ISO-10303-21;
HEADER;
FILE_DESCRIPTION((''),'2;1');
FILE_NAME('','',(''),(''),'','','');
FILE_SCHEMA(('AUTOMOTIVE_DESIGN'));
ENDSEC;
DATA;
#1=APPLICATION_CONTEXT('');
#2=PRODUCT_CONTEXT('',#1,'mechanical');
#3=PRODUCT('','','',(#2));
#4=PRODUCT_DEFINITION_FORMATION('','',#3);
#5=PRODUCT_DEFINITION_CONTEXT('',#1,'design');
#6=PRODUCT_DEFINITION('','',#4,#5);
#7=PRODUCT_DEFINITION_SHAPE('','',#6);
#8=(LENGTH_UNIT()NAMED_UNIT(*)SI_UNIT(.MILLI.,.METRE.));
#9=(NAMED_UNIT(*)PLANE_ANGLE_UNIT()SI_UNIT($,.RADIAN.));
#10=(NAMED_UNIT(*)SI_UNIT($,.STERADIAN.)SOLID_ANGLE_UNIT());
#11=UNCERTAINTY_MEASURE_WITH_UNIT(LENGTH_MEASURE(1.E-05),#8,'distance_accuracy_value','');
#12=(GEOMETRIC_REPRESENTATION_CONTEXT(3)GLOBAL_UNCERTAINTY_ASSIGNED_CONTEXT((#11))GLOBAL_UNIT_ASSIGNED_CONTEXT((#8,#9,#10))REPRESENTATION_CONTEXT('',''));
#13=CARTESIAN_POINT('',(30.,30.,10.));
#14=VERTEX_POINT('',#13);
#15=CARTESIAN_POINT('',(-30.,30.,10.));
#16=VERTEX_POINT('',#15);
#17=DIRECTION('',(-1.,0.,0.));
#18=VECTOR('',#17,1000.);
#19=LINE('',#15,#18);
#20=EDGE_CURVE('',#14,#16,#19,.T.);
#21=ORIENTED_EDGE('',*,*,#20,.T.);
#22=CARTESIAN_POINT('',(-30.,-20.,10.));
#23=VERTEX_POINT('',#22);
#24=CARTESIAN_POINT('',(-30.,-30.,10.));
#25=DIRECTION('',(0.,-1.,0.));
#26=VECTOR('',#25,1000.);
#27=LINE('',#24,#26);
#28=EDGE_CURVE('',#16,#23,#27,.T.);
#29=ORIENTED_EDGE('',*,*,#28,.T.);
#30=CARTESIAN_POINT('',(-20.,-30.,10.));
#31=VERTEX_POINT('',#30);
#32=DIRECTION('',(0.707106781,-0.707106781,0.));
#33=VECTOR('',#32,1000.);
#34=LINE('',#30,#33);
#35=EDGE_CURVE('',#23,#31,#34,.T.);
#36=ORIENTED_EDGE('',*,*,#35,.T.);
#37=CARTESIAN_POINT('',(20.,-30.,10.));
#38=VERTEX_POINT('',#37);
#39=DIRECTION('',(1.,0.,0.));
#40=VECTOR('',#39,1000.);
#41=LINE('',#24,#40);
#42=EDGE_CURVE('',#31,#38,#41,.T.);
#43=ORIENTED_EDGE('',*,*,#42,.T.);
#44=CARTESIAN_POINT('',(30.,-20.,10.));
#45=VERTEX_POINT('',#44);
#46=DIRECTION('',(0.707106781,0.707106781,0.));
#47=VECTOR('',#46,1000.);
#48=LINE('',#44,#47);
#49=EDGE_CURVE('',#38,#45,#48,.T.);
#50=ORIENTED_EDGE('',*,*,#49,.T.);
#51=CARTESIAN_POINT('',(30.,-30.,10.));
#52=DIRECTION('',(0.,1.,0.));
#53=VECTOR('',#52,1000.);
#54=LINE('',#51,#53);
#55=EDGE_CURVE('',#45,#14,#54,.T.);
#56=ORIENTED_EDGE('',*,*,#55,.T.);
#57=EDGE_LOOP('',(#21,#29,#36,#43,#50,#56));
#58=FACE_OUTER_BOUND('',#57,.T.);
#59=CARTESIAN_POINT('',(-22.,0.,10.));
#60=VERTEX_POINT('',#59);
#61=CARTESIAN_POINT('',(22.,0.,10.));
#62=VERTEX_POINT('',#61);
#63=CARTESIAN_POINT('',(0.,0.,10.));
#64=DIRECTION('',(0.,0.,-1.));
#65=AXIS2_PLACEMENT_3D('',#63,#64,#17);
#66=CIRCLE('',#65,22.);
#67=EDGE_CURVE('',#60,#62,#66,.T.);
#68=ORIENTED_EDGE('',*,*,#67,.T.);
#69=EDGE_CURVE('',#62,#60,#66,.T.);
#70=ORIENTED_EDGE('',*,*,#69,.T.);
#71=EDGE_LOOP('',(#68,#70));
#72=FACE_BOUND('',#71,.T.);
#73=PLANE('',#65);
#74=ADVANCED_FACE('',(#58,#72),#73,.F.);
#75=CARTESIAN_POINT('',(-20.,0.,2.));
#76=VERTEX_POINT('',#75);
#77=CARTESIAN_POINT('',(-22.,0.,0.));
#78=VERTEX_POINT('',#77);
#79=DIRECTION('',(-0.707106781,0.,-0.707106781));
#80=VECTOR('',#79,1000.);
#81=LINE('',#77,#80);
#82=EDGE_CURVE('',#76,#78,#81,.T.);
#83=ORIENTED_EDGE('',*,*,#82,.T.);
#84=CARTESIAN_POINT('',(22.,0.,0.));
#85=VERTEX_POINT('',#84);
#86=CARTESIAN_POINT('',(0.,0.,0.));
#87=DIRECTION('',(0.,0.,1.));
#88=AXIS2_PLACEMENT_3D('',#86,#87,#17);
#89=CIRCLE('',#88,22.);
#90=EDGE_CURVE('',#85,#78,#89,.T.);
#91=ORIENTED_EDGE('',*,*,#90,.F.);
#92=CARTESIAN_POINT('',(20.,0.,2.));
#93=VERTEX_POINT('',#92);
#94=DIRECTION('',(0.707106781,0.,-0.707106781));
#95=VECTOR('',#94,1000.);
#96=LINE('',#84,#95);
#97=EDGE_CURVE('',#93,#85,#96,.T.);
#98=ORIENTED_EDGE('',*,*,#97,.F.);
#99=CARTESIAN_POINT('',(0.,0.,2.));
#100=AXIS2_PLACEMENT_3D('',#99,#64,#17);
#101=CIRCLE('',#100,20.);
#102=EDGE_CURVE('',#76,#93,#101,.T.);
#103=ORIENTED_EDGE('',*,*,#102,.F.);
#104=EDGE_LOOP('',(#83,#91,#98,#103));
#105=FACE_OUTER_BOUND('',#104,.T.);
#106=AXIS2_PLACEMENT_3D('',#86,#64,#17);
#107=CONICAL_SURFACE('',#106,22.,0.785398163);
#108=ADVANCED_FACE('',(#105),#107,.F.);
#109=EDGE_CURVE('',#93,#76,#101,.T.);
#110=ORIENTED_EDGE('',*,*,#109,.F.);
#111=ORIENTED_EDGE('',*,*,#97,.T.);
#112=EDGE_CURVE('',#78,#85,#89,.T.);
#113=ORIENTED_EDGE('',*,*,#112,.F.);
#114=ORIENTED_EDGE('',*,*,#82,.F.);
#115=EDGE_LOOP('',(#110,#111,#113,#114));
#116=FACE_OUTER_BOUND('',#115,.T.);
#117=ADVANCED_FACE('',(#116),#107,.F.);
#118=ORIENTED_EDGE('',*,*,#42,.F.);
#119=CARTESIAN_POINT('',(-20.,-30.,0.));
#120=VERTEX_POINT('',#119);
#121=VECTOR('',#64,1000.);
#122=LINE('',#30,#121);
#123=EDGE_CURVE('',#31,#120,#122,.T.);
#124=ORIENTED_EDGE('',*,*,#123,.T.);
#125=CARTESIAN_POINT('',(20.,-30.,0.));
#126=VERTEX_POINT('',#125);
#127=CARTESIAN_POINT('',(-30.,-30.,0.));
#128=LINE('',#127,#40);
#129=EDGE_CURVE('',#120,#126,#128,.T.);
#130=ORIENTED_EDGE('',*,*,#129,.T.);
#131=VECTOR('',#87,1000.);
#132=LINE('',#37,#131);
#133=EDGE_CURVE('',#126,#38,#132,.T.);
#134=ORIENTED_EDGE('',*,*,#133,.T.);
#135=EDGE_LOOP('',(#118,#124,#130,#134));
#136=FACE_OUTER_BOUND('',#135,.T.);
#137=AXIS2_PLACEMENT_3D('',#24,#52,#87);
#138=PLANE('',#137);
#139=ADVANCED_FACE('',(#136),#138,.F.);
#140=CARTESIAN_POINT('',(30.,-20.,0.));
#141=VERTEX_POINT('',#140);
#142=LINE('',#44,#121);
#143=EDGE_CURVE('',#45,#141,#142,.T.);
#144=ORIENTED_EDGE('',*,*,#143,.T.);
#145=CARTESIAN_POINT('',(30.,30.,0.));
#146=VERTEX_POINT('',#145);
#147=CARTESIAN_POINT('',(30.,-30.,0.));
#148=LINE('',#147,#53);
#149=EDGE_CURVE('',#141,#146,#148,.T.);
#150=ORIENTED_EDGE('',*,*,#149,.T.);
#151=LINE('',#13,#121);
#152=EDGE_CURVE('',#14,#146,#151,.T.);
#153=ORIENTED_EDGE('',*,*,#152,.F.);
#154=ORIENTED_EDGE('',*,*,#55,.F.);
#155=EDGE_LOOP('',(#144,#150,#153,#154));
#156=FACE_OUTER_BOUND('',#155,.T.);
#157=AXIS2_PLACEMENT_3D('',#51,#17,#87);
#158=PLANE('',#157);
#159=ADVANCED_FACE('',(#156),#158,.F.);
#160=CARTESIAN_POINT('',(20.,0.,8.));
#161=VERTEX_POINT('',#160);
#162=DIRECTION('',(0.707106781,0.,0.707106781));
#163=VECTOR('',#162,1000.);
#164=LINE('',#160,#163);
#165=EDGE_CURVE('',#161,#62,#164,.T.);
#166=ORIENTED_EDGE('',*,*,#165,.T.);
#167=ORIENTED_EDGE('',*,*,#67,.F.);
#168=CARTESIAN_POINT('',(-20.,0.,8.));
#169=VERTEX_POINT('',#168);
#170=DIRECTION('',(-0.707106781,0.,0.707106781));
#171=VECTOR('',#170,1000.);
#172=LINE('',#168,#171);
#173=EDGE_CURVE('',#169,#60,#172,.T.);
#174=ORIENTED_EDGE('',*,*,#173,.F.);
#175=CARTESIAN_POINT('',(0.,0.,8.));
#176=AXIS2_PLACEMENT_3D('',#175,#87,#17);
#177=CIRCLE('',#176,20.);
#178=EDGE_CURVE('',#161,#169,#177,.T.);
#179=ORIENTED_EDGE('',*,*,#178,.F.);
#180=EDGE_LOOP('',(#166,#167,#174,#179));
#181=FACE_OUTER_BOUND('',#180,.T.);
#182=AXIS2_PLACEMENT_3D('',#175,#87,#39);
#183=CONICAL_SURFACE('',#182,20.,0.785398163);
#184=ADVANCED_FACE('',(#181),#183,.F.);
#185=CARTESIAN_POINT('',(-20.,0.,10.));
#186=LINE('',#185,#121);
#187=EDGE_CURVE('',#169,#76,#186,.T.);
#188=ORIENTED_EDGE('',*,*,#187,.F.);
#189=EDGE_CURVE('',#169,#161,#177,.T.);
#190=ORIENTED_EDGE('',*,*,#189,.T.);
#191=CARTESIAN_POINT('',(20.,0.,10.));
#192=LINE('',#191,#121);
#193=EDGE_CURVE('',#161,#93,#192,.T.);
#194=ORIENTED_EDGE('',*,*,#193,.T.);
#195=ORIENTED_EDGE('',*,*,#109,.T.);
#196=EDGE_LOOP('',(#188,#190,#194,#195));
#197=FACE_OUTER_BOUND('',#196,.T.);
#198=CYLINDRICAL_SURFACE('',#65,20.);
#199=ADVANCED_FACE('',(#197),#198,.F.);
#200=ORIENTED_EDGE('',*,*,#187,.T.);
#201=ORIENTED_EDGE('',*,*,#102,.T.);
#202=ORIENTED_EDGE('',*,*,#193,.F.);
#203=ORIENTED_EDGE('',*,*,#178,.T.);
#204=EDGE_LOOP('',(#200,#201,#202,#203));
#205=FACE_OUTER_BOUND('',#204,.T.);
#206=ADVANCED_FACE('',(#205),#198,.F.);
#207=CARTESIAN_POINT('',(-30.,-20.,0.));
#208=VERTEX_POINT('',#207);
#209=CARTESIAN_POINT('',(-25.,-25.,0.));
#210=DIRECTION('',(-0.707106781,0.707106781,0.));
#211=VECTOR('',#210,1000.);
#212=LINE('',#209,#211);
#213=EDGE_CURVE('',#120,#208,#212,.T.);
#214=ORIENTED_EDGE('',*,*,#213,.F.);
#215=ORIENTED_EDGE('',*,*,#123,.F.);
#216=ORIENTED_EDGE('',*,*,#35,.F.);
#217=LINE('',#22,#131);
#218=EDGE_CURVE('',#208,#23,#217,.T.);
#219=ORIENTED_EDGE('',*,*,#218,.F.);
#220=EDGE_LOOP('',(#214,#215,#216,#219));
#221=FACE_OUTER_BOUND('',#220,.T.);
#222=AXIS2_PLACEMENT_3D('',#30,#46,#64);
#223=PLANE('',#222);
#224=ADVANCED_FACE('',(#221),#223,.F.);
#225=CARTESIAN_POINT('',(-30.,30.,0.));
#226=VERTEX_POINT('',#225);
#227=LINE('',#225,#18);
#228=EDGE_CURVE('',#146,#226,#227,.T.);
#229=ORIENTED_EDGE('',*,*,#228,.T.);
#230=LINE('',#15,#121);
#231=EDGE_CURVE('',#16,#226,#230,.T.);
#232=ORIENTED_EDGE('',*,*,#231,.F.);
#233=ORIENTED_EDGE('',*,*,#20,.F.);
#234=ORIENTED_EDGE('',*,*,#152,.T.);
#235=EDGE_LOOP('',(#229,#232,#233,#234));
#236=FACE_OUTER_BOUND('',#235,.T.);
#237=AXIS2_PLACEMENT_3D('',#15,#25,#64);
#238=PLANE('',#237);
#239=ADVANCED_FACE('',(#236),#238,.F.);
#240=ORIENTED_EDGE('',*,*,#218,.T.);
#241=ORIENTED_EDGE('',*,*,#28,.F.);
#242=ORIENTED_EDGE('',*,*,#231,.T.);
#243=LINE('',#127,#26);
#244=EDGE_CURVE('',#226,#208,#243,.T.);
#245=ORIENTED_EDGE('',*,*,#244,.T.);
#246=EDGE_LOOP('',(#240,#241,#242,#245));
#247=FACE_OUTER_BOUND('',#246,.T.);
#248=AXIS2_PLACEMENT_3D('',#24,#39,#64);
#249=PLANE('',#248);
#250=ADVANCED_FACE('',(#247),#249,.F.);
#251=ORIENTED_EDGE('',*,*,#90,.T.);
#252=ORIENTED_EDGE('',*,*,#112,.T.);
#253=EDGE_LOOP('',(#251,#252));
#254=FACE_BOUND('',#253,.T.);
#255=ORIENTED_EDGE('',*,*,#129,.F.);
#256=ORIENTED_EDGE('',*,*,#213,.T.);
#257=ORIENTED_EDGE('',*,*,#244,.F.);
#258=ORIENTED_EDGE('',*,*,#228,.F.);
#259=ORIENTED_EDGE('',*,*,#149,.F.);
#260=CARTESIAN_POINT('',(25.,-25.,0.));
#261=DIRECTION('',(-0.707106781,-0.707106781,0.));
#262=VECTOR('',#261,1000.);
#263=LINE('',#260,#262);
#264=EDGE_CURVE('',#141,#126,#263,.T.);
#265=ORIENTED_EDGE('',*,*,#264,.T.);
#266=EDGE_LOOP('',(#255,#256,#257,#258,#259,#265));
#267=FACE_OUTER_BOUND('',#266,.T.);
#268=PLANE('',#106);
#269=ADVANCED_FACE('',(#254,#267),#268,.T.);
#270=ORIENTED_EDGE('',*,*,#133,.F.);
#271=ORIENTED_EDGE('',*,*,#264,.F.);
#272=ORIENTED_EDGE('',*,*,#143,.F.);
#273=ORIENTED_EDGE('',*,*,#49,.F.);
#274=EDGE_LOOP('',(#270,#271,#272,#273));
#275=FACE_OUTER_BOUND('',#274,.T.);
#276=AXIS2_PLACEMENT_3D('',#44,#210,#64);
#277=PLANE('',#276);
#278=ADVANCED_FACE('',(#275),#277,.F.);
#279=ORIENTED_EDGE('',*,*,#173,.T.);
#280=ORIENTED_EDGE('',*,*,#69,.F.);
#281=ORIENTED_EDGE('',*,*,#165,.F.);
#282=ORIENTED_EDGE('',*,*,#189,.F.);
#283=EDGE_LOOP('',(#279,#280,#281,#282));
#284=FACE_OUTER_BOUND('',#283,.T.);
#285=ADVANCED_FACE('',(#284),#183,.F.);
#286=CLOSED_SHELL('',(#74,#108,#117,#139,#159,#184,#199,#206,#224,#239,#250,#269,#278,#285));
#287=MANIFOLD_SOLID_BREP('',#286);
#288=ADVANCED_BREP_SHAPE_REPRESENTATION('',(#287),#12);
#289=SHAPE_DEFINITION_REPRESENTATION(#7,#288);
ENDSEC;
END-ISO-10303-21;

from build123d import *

# Parameters (mm, degrees)
SKETCH_1_W      = 60
SKETCH_1_H      = 60
SKETCH_1_R      = 20
EXTRUDE_1_DEPTH = 10
CHAMFER_1_SIZE  = 10
CHAMFER_3_SIZE  = 2


with BuildPart() as part:
    # 草图1 → 凸台-拉伸1 (new body)
    with BuildSketch(Plane.XY):
        Rectangle(SKETCH_1_W, SKETCH_1_H)
        Circle(SKETCH_1_R, mode=Mode.SUBTRACT)
    extrude(amount=EXTRUDE_1_DEPTH)

    # 倒角1
    chamfer_1_edges = [part.edges().sort_by_distance(p)[0] for p in [
        (30, -30, 5),
        (-30, -30, 5),
    ]]
    chamfer(chamfer_1_edges, length=CHAMFER_1_SIZE)

    # 倒角3
    chamfer_3_edges = [part.edges().sort_by_distance(p)[0] for p in [
        (-20, 0, 0),
        (-20, 0, 10),
    ]]
    chamfer(chamfer_3_edges, length=CHAMFER_3_SIZE)


solid = part.part
